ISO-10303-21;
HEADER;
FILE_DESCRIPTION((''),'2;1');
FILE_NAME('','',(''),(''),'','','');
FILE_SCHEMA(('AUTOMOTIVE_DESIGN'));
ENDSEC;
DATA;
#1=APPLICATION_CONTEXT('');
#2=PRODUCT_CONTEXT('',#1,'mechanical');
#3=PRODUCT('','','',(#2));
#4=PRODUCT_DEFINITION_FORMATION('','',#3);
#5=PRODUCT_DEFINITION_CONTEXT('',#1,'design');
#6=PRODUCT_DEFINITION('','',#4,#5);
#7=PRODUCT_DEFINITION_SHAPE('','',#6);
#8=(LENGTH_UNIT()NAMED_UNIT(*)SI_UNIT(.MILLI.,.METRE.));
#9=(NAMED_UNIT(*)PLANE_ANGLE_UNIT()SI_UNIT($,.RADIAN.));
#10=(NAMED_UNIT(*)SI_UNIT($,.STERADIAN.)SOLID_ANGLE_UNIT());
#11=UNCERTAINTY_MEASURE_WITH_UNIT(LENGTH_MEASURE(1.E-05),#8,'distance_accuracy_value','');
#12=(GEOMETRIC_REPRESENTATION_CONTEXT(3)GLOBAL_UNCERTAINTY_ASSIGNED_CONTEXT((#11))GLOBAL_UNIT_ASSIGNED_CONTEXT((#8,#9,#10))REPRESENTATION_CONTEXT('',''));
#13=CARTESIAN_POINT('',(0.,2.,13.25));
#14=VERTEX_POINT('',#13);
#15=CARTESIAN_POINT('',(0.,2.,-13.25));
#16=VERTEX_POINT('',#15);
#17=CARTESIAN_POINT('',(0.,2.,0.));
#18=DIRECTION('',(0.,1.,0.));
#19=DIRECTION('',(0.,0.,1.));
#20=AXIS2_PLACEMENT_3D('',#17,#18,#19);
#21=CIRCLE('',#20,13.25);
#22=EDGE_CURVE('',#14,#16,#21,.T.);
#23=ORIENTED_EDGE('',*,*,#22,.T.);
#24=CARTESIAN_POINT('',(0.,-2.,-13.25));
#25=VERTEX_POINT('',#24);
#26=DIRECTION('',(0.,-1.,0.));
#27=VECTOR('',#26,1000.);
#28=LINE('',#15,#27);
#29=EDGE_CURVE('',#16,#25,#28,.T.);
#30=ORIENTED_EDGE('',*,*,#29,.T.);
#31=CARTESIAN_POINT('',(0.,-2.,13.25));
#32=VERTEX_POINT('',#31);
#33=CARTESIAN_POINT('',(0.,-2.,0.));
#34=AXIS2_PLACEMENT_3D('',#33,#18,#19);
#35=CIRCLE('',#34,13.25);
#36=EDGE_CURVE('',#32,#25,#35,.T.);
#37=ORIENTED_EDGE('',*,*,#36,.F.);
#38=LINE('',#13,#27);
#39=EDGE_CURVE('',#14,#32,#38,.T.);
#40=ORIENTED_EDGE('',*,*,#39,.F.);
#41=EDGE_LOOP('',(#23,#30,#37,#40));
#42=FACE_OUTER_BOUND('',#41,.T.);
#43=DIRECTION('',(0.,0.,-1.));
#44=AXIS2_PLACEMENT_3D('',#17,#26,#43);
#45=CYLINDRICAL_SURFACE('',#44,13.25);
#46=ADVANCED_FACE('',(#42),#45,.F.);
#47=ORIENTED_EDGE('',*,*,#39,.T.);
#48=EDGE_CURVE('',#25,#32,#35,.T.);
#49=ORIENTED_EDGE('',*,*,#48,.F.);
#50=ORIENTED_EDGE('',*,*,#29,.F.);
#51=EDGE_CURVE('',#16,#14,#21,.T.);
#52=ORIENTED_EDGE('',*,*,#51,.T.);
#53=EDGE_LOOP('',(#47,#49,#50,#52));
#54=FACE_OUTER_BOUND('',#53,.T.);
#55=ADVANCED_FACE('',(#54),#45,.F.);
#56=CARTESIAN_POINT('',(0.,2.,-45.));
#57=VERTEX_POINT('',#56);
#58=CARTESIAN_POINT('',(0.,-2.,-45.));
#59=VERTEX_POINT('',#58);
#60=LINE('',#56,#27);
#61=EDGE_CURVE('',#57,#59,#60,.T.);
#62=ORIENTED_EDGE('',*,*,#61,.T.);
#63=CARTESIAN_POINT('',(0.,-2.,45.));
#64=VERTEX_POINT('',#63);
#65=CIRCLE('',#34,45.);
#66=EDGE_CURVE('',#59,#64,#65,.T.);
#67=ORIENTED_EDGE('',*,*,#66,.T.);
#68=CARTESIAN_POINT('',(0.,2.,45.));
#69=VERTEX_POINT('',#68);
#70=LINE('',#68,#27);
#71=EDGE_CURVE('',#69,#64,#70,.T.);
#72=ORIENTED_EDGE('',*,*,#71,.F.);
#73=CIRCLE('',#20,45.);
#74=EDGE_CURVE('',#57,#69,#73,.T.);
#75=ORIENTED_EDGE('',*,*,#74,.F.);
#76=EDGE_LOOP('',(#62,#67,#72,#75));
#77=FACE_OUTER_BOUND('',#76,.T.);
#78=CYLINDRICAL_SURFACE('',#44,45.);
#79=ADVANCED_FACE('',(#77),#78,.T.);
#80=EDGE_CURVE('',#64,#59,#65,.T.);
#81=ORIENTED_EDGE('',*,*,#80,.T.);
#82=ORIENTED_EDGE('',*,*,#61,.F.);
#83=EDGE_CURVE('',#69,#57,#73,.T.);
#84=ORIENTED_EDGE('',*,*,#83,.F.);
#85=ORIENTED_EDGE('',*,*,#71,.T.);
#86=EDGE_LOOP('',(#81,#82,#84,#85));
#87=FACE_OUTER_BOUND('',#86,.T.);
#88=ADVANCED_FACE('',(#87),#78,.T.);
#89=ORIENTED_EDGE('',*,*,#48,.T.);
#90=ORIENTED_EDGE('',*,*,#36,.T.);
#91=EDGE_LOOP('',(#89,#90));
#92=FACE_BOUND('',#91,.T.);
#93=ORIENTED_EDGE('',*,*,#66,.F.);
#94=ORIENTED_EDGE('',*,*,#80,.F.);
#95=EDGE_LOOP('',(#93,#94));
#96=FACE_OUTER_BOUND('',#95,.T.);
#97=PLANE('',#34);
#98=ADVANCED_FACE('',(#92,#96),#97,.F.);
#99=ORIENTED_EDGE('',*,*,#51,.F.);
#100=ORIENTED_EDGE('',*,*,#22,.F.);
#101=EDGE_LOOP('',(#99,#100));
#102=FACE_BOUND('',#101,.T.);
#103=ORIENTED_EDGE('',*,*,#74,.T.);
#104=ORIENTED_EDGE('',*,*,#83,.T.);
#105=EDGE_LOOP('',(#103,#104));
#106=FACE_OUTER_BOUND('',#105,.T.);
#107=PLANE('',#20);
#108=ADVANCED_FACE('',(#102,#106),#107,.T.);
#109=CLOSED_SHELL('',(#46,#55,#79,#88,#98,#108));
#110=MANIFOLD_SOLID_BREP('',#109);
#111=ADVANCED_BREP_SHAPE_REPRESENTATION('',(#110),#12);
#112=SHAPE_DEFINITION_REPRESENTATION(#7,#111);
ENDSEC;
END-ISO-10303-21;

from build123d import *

# Parameters (mm, degrees)
SKETCH_1_R      = 45
SKETCH_1_R_2    = 13.25
EXTRUDE_1_DEPTH = 2


with BuildPart() as part:
    # 草图1 → 凸台-拉伸1 (new, symmetric)
    with BuildSketch(Plane(origin=(0, 0, 0), x_dir=(1, 0, 0), z_dir=(0, 1, 0))):
        with Locations(Location((0, 0, 0), (0, 0, 270))):
            Circle(SKETCH_1_R)
        with Locations(Location((0, 0, 0), (0, 0, 270))):
            Circle(SKETCH_1_R_2, mode=Mode.SUBTRACT)
    extrude(amount=EXTRUDE_1_DEPTH, both=True)


solid = part.part
